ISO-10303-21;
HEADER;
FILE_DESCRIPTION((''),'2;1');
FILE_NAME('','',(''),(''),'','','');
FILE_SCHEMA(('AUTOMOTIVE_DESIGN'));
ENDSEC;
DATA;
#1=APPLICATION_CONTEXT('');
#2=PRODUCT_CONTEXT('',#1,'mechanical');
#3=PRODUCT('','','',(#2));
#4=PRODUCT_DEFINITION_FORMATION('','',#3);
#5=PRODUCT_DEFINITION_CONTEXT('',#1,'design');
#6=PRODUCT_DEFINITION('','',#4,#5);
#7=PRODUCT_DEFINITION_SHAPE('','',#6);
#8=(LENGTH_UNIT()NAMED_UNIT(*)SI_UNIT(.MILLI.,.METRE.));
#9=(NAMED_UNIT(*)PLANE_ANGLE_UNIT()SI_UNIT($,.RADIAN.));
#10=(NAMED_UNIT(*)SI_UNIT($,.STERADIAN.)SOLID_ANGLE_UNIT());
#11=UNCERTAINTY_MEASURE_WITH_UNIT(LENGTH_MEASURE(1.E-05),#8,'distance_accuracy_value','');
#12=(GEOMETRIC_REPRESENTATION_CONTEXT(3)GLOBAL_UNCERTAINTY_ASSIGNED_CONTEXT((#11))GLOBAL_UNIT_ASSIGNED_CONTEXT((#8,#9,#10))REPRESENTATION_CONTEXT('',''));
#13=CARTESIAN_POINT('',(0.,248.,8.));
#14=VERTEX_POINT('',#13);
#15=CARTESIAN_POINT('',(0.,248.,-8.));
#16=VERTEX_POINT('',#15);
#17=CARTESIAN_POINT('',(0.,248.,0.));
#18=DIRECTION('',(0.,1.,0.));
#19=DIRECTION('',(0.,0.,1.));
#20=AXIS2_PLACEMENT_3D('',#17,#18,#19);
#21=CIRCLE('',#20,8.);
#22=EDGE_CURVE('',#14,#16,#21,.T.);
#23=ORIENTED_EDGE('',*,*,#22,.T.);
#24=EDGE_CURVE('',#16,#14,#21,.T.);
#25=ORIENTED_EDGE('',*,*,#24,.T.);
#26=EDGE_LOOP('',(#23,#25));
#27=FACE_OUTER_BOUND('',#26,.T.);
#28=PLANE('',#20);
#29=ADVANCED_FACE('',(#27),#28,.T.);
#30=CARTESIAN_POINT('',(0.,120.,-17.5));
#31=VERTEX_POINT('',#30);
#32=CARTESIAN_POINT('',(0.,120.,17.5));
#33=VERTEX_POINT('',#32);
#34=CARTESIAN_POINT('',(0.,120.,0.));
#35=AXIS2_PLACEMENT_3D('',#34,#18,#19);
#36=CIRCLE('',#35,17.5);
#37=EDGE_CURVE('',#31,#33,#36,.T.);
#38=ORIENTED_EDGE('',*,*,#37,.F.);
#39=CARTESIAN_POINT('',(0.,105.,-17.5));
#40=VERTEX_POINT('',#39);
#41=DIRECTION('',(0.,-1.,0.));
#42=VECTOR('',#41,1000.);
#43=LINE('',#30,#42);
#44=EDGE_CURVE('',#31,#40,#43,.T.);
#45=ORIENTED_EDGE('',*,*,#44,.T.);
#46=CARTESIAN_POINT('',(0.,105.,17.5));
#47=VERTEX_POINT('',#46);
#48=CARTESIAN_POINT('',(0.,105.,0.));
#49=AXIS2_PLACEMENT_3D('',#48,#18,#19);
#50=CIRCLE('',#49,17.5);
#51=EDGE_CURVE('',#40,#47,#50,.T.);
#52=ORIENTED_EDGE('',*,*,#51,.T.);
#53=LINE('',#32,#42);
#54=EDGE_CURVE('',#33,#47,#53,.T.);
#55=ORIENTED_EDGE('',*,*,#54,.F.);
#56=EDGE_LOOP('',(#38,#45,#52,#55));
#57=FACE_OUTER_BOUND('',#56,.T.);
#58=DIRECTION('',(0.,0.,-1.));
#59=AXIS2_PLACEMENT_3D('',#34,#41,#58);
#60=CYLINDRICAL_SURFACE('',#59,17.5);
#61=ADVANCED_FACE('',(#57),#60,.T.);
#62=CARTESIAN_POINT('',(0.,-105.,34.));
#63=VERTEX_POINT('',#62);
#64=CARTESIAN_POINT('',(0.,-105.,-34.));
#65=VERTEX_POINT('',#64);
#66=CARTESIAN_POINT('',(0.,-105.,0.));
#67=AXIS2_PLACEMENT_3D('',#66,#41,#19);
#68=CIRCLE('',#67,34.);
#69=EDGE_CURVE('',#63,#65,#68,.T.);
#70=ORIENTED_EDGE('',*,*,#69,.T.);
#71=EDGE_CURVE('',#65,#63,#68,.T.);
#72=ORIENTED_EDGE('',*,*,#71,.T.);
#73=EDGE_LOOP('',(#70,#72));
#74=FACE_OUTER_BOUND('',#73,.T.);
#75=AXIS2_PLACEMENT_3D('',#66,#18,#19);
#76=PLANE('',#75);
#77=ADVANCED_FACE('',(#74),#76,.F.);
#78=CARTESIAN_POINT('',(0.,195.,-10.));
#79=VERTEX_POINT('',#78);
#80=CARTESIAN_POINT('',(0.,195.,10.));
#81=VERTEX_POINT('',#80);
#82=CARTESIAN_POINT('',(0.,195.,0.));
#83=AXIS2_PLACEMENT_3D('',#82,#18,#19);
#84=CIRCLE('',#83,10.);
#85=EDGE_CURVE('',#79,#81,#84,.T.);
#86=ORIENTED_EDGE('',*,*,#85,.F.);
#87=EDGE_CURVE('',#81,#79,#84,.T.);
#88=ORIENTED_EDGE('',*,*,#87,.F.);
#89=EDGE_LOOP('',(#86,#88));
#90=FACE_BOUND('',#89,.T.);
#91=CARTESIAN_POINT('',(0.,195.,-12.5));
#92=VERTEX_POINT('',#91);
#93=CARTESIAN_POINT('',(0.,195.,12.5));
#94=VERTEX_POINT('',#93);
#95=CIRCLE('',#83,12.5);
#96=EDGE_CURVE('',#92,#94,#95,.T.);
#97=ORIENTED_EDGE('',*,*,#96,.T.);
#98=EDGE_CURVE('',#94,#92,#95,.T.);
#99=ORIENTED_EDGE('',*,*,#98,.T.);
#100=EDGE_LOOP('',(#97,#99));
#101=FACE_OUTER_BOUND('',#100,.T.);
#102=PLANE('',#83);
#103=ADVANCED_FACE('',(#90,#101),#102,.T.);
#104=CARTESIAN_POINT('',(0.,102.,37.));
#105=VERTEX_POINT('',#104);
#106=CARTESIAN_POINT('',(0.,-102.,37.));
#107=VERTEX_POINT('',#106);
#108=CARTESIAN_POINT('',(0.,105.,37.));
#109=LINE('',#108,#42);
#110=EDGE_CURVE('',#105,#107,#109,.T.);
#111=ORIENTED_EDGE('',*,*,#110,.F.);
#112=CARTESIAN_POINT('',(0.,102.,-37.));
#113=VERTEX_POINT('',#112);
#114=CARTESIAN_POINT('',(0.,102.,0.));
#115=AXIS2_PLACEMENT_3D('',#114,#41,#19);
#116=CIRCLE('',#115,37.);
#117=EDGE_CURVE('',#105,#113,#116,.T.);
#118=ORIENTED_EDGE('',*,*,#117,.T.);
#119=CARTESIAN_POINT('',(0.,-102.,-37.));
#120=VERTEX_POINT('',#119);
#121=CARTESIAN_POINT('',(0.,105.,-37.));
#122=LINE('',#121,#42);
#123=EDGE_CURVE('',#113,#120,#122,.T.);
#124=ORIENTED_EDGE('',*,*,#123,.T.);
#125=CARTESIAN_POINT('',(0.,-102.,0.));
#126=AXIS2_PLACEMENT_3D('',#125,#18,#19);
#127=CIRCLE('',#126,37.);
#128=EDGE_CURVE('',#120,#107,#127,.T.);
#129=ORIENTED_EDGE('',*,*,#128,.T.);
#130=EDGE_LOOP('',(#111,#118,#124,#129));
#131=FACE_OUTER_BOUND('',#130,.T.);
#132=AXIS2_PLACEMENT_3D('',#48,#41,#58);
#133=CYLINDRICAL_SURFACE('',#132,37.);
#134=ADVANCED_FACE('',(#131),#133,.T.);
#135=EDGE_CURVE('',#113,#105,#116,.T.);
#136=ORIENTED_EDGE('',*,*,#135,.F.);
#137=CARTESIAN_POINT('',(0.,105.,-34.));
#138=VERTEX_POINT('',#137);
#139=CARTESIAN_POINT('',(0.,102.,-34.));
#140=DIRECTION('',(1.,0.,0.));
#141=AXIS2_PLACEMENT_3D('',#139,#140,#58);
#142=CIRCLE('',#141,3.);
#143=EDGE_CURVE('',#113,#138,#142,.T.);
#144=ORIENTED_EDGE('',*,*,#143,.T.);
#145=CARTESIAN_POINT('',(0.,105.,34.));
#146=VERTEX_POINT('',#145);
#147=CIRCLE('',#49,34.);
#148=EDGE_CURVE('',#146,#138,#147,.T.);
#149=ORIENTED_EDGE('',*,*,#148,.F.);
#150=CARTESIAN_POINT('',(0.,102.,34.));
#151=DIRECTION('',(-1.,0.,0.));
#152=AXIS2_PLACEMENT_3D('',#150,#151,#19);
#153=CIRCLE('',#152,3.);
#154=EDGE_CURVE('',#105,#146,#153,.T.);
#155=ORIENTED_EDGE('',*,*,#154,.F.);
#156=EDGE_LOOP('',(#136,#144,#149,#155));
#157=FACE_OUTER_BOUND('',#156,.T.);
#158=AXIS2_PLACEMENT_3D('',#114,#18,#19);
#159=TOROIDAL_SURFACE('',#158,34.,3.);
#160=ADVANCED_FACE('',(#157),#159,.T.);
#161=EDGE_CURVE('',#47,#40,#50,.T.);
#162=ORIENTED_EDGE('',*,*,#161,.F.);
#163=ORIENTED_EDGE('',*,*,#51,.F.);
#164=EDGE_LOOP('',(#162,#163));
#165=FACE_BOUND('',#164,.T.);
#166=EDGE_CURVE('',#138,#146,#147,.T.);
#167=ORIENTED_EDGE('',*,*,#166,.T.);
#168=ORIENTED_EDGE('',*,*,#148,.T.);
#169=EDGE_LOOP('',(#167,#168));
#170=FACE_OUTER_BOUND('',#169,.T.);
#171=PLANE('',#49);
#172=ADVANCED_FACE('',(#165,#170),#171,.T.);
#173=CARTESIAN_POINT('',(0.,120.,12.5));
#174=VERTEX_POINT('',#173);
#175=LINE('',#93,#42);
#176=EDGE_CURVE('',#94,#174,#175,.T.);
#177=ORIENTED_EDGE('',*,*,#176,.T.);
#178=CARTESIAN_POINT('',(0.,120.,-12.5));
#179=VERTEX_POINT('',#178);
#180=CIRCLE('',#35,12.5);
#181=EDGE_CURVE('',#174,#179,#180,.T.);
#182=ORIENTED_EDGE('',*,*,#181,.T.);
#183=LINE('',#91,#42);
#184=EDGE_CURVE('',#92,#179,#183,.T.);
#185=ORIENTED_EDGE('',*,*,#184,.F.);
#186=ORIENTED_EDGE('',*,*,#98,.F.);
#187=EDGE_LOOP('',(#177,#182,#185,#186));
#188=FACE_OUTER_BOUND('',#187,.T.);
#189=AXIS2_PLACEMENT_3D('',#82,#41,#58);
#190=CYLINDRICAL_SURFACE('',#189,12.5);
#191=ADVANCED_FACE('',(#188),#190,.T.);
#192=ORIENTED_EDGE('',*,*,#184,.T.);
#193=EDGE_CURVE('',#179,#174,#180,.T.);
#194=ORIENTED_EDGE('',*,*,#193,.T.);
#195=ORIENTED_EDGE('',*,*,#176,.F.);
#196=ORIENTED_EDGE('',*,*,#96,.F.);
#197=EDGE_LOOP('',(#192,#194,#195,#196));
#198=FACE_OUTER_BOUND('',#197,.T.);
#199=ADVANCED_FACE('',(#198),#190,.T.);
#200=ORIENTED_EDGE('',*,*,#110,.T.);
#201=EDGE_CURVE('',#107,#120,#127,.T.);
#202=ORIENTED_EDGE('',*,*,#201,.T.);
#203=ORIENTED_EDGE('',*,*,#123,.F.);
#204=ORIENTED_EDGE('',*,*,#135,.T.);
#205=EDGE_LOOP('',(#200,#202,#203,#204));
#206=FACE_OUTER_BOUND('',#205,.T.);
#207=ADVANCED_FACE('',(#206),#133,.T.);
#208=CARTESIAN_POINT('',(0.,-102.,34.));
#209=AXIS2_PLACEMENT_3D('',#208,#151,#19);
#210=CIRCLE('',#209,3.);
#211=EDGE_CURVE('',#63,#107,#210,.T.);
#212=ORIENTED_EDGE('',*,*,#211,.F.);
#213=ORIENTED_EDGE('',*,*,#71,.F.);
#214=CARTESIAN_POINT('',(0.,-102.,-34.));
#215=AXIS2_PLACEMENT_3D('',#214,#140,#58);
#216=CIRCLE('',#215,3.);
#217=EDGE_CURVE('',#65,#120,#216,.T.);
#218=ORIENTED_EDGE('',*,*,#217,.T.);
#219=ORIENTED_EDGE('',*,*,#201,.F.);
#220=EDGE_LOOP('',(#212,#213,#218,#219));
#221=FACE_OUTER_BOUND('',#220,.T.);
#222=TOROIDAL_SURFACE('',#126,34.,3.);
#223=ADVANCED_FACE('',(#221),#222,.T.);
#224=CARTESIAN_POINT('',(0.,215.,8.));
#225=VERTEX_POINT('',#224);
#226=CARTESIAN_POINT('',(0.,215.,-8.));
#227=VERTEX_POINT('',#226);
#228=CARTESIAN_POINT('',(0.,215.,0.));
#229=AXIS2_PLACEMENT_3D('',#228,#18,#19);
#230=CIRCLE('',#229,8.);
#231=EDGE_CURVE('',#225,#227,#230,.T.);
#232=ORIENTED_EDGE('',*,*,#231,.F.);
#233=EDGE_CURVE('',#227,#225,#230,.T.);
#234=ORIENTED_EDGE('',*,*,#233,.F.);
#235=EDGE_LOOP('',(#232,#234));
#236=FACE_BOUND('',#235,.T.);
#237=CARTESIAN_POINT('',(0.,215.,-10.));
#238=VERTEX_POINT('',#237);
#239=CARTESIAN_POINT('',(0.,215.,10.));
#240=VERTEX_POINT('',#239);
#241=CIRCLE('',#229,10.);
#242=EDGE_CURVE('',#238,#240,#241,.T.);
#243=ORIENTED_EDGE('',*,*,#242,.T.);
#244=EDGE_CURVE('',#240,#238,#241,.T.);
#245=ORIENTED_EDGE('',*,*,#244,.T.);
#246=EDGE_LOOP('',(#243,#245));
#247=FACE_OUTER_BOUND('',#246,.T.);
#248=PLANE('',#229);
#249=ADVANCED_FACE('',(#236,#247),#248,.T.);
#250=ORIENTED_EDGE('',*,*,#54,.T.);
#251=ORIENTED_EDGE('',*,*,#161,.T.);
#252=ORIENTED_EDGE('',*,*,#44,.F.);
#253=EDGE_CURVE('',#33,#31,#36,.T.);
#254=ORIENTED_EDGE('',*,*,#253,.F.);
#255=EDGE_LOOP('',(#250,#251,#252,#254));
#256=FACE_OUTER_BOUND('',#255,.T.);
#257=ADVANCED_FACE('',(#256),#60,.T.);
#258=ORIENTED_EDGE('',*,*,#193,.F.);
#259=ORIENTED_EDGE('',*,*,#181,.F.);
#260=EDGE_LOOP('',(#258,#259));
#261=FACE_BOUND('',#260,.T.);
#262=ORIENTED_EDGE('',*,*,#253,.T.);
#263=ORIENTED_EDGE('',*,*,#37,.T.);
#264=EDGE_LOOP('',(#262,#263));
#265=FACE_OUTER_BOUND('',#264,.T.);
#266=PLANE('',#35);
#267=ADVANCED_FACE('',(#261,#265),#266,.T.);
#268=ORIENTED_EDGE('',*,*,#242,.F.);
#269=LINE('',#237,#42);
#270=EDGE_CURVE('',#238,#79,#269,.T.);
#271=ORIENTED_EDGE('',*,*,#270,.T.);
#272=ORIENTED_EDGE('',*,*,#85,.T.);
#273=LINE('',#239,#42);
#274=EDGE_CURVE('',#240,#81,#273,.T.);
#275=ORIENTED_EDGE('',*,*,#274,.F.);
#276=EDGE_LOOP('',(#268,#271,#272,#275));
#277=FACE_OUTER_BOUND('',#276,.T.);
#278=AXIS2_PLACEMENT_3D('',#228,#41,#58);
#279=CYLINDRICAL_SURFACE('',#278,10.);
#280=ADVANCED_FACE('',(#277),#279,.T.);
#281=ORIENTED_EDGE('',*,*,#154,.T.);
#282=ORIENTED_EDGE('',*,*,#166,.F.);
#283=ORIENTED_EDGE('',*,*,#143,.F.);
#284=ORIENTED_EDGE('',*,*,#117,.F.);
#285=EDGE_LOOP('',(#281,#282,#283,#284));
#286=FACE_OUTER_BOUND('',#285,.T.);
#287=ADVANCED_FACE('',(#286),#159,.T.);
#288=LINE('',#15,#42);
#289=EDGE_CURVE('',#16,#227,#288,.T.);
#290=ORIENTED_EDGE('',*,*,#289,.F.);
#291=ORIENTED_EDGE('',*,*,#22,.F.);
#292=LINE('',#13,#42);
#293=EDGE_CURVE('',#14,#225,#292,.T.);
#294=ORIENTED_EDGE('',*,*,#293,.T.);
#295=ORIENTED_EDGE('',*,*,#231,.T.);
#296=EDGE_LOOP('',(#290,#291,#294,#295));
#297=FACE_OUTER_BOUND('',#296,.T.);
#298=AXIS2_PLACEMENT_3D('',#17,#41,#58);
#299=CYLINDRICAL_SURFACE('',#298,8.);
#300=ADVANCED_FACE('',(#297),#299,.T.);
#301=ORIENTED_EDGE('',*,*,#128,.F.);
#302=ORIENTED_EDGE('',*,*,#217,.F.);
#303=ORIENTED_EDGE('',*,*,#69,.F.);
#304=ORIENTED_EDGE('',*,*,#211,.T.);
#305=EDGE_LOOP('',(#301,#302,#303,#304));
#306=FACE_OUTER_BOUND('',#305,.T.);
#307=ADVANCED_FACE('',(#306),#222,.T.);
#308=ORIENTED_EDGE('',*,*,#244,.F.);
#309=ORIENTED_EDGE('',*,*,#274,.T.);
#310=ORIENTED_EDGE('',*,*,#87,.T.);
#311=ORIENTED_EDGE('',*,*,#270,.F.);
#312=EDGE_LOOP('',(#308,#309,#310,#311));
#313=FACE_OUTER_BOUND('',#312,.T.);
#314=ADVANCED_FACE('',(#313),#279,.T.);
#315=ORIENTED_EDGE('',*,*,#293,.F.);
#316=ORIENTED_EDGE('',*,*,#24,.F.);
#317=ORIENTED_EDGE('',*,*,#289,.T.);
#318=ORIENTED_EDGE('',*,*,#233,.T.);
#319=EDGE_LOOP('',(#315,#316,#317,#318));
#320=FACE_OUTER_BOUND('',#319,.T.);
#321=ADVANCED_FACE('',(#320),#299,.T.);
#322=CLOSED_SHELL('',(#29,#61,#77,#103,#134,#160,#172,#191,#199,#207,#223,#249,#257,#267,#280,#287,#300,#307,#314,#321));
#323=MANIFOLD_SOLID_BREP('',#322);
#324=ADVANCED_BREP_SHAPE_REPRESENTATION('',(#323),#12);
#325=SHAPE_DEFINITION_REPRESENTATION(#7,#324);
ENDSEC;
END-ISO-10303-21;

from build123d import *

# Parameters (mm, degrees)
SKETCH_1_R      = 37
EXTRUDE_1_DEPTH = 105
SKETCH_2_R      = 17.5
EXTRUDE_2_DEPTH = 15
SKETCH_3_R      = 12.5
EXTRUDE_3_DEPTH = 75
SKETCH_4_R      = 10
EXTRUDE_4_DEPTH = 20
SKETCH_5_R      = 8
EXTRUDE_5_DEPTH = 33
FILLET_1_R      = 3


with BuildPart() as part:
    # 草图1 → 凸台-拉伸1 (new, symmetric)
    with BuildSketch(Plane(origin=(0, 0, 0), x_dir=(1, 0, 0), z_dir=(0, 1, 0))):
        with Locations(Location((0, 0, 0), (0, 0, 270))):
            Circle(SKETCH_1_R)
    extrude(amount=EXTRUDE_1_DEPTH, both=True)

    # 草图2 → 凸台-拉伸2 (add)
    with BuildSketch(Plane(origin=(0, 105, 0), x_dir=(1, 0, 0), z_dir=(0, 1, 0))):
        with Locations(Location((0, 0, 0), (0, 0, 270))):
            Circle(SKETCH_2_R)
    extrude(amount=EXTRUDE_2_DEPTH)

    # 草图3 → 凸台-拉伸3 (add)
    with BuildSketch(Plane(origin=(0, 120, 0), x_dir=(1, 0, 0), z_dir=(0, 1, 0))):
        with Locations(Location((0, 0, 0), (0, 0, 270))):
            Circle(SKETCH_3_R)
    extrude(amount=EXTRUDE_3_DEPTH)

    # 草图4 → 凸台-拉伸4 (add)
    with BuildSketch(Plane(origin=(0, 195, 0), x_dir=(1, 0, 0), z_dir=(0, 1, 0))):
        with Locations(Location((0, 0, 0), (0, 0, 270))):
            Circle(SKETCH_4_R)
    extrude(amount=EXTRUDE_4_DEPTH)

    # 草图5 → 凸台-拉伸5 (add)
    with BuildSketch(Plane(origin=(0, 215, 0), x_dir=(1, 0, 0), z_dir=(0, 1, 0))):
        with Locations(Location((0, 0, 0), (0, 0, 270))):
            Circle(SKETCH_5_R)
    extrude(amount=EXTRUDE_5_DEPTH)

    # 圆角1
    fillet_1_edges = [part.edges().sort_by_distance(p)[0] for p in [
        (0, -105, -37),
        (0, 105, -37),
    ]]
    fillet(fillet_1_edges, radius=FILLET_1_R)


solid = part.part
